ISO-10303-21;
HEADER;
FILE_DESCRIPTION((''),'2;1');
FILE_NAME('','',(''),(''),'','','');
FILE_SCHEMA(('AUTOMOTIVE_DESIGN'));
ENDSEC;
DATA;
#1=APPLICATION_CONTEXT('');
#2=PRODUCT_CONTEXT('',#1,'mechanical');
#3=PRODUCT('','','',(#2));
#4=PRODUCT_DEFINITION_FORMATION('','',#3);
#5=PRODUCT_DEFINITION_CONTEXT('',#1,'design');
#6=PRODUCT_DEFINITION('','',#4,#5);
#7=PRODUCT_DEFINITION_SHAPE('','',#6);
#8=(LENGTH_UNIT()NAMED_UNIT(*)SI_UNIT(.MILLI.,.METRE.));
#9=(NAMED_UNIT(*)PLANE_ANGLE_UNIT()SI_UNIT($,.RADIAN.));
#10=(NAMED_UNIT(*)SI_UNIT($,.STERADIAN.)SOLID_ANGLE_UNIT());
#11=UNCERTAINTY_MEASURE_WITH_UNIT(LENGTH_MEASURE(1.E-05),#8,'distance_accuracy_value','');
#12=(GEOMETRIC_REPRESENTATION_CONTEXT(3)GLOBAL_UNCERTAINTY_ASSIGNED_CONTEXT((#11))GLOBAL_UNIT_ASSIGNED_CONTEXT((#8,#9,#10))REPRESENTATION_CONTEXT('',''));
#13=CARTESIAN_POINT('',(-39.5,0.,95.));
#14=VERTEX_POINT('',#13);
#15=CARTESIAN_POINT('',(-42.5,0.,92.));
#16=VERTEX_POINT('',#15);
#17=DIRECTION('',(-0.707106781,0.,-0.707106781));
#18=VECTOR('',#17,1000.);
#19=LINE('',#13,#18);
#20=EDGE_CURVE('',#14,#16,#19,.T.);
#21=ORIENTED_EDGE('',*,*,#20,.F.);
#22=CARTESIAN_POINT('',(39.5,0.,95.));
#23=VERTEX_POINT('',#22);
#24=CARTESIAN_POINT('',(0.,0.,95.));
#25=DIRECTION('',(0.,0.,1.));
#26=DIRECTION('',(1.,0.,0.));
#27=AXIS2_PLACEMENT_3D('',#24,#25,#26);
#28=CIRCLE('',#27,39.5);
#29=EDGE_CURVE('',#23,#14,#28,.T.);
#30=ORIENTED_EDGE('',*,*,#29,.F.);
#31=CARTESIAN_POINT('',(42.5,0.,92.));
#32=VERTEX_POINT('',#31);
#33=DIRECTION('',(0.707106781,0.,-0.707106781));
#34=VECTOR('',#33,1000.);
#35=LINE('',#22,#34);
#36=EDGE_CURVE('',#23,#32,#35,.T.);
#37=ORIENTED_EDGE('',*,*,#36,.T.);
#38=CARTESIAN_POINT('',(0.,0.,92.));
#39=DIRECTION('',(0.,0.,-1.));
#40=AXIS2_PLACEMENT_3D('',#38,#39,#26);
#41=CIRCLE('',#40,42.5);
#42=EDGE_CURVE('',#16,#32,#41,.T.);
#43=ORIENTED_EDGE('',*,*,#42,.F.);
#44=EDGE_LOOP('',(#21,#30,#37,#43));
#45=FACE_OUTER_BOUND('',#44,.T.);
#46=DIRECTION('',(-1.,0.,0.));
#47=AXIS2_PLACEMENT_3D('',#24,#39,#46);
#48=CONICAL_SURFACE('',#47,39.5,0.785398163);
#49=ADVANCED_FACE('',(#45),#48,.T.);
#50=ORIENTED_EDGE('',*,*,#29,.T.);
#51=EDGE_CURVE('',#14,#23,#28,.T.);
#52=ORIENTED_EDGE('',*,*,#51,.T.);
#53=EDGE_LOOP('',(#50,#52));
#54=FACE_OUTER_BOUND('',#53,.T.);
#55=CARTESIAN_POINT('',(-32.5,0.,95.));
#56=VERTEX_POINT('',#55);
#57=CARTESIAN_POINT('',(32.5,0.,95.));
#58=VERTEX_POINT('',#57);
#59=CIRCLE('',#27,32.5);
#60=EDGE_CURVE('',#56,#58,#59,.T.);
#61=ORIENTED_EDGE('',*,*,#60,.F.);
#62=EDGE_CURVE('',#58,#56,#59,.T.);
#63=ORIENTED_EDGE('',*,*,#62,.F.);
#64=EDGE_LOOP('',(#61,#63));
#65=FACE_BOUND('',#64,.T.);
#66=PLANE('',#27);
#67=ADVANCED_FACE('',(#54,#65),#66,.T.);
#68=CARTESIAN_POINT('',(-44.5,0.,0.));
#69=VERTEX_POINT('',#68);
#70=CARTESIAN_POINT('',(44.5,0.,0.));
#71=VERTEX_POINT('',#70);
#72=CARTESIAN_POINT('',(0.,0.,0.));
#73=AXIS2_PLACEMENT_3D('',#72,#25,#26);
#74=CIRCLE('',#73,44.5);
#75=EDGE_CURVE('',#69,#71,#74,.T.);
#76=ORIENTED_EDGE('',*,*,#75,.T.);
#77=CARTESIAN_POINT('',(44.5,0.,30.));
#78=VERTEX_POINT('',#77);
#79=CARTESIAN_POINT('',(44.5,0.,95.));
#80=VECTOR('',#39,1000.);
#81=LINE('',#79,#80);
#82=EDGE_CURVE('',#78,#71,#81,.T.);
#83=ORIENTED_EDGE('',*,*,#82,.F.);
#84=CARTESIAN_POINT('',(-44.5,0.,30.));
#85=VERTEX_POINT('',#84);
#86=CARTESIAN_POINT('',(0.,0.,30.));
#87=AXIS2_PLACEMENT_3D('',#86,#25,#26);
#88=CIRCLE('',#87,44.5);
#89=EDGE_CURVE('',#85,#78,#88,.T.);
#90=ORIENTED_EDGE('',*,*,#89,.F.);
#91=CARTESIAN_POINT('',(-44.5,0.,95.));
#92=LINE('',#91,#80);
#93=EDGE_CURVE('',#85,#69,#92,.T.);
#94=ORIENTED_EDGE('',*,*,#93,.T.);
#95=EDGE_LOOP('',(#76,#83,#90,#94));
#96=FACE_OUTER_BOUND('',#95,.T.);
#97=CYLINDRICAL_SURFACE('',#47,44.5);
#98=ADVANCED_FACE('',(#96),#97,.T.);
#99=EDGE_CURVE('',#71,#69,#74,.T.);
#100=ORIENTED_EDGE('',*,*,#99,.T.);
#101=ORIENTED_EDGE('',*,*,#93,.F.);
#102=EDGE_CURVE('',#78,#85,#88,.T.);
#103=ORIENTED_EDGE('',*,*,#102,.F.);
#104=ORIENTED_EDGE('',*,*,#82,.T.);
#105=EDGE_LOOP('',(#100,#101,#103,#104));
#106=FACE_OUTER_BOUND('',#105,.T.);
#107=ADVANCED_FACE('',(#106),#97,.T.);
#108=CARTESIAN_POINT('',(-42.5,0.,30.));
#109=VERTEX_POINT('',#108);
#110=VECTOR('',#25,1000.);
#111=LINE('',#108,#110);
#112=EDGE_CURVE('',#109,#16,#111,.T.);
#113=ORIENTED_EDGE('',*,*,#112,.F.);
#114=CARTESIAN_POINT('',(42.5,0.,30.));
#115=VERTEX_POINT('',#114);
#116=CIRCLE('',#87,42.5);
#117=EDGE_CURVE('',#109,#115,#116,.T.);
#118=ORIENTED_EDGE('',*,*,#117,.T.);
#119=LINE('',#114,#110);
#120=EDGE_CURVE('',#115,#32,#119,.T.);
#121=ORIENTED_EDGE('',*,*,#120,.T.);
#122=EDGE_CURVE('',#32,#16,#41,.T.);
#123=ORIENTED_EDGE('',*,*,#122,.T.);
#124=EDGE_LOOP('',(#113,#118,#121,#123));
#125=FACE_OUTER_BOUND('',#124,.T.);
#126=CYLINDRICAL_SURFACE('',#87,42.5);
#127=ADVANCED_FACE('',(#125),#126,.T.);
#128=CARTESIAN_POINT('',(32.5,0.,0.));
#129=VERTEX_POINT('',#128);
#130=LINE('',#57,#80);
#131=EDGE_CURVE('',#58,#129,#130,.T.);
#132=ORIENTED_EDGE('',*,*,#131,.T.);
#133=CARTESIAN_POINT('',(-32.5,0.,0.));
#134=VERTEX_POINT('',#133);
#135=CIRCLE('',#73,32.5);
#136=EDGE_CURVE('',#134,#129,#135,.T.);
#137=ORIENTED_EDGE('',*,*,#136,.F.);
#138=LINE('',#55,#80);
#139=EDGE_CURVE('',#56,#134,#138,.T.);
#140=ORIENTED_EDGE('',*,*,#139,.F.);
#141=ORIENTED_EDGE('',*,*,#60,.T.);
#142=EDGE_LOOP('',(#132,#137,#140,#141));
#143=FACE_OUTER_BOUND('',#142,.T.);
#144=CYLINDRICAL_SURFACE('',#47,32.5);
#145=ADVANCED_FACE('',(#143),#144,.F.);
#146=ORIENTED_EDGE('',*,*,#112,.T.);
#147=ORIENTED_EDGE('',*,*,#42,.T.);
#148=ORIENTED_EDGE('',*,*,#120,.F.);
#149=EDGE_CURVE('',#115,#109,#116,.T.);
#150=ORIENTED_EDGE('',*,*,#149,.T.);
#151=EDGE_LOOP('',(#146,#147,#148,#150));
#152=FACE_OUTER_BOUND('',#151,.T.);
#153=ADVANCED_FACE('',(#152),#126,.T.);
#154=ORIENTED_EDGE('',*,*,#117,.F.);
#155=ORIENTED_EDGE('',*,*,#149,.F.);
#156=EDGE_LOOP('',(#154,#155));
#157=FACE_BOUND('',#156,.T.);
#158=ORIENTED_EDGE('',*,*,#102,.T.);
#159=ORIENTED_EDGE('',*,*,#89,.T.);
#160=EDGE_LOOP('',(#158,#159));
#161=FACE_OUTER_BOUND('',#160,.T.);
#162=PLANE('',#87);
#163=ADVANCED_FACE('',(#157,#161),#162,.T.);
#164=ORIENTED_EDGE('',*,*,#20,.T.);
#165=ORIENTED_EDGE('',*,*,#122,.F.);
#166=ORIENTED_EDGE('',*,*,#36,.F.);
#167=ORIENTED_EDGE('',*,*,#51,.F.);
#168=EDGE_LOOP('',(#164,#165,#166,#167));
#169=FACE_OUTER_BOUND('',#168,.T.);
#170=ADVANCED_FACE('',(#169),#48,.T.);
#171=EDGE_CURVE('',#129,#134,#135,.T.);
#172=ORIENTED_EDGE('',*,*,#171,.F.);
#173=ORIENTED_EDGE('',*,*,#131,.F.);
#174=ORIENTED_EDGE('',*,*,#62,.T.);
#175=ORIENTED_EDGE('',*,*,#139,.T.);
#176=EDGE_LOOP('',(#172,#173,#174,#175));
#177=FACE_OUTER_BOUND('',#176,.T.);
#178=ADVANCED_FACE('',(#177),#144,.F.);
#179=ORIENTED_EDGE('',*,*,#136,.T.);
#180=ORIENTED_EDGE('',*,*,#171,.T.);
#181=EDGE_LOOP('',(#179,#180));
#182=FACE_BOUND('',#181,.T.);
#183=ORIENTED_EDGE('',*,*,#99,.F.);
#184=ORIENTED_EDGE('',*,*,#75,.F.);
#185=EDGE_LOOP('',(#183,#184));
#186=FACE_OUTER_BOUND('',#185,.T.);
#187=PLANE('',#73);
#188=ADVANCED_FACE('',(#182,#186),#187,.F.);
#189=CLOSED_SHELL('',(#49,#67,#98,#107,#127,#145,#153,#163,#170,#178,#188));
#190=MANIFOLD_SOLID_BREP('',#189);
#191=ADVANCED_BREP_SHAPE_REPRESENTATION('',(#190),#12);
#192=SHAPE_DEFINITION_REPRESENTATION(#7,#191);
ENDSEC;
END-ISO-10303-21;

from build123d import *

# Parameters (mm, degrees)
SKETCH_1_R          = 44.5
SKETCH_1_R_2        = 32.5
EXTRUDE_1_DEPTH     = 95
CUT_EXTRUDE_START   = -65
SKETCH_2_R          = 44.5
SKETCH_2_R_2        = 42.5
CUT_EXTRUDE_1_DEPTH = 65
CHAMFER_1_SIZE      = 3


with BuildPart() as part:
    # 草图1 → 凸台-拉伸1 (new body)
    with BuildSketch(Plane.XY):
        Circle(SKETCH_1_R)
        Circle(SKETCH_1_R_2, mode=Mode.SUBTRACT)
    extrude(amount=EXTRUDE_1_DEPTH)

    # 草图2 → 切除-拉伸1 (cut)
    with BuildSketch(Plane.XY.offset(95).offset(CUT_EXTRUDE_START)):
        Circle(SKETCH_2_R)
        Circle(SKETCH_2_R_2, mode=Mode.SUBTRACT)
    extrude(amount=CUT_EXTRUDE_1_DEPTH, mode=Mode.SUBTRACT)

    # 倒角1
    chamfer_1_edges = [part.edges().sort_by_distance(p)[0] for p in [
        (-42.5, 0, 95),
    ]]
    chamfer(chamfer_1_edges, length=CHAMFER_1_SIZE)


solid = part.part
